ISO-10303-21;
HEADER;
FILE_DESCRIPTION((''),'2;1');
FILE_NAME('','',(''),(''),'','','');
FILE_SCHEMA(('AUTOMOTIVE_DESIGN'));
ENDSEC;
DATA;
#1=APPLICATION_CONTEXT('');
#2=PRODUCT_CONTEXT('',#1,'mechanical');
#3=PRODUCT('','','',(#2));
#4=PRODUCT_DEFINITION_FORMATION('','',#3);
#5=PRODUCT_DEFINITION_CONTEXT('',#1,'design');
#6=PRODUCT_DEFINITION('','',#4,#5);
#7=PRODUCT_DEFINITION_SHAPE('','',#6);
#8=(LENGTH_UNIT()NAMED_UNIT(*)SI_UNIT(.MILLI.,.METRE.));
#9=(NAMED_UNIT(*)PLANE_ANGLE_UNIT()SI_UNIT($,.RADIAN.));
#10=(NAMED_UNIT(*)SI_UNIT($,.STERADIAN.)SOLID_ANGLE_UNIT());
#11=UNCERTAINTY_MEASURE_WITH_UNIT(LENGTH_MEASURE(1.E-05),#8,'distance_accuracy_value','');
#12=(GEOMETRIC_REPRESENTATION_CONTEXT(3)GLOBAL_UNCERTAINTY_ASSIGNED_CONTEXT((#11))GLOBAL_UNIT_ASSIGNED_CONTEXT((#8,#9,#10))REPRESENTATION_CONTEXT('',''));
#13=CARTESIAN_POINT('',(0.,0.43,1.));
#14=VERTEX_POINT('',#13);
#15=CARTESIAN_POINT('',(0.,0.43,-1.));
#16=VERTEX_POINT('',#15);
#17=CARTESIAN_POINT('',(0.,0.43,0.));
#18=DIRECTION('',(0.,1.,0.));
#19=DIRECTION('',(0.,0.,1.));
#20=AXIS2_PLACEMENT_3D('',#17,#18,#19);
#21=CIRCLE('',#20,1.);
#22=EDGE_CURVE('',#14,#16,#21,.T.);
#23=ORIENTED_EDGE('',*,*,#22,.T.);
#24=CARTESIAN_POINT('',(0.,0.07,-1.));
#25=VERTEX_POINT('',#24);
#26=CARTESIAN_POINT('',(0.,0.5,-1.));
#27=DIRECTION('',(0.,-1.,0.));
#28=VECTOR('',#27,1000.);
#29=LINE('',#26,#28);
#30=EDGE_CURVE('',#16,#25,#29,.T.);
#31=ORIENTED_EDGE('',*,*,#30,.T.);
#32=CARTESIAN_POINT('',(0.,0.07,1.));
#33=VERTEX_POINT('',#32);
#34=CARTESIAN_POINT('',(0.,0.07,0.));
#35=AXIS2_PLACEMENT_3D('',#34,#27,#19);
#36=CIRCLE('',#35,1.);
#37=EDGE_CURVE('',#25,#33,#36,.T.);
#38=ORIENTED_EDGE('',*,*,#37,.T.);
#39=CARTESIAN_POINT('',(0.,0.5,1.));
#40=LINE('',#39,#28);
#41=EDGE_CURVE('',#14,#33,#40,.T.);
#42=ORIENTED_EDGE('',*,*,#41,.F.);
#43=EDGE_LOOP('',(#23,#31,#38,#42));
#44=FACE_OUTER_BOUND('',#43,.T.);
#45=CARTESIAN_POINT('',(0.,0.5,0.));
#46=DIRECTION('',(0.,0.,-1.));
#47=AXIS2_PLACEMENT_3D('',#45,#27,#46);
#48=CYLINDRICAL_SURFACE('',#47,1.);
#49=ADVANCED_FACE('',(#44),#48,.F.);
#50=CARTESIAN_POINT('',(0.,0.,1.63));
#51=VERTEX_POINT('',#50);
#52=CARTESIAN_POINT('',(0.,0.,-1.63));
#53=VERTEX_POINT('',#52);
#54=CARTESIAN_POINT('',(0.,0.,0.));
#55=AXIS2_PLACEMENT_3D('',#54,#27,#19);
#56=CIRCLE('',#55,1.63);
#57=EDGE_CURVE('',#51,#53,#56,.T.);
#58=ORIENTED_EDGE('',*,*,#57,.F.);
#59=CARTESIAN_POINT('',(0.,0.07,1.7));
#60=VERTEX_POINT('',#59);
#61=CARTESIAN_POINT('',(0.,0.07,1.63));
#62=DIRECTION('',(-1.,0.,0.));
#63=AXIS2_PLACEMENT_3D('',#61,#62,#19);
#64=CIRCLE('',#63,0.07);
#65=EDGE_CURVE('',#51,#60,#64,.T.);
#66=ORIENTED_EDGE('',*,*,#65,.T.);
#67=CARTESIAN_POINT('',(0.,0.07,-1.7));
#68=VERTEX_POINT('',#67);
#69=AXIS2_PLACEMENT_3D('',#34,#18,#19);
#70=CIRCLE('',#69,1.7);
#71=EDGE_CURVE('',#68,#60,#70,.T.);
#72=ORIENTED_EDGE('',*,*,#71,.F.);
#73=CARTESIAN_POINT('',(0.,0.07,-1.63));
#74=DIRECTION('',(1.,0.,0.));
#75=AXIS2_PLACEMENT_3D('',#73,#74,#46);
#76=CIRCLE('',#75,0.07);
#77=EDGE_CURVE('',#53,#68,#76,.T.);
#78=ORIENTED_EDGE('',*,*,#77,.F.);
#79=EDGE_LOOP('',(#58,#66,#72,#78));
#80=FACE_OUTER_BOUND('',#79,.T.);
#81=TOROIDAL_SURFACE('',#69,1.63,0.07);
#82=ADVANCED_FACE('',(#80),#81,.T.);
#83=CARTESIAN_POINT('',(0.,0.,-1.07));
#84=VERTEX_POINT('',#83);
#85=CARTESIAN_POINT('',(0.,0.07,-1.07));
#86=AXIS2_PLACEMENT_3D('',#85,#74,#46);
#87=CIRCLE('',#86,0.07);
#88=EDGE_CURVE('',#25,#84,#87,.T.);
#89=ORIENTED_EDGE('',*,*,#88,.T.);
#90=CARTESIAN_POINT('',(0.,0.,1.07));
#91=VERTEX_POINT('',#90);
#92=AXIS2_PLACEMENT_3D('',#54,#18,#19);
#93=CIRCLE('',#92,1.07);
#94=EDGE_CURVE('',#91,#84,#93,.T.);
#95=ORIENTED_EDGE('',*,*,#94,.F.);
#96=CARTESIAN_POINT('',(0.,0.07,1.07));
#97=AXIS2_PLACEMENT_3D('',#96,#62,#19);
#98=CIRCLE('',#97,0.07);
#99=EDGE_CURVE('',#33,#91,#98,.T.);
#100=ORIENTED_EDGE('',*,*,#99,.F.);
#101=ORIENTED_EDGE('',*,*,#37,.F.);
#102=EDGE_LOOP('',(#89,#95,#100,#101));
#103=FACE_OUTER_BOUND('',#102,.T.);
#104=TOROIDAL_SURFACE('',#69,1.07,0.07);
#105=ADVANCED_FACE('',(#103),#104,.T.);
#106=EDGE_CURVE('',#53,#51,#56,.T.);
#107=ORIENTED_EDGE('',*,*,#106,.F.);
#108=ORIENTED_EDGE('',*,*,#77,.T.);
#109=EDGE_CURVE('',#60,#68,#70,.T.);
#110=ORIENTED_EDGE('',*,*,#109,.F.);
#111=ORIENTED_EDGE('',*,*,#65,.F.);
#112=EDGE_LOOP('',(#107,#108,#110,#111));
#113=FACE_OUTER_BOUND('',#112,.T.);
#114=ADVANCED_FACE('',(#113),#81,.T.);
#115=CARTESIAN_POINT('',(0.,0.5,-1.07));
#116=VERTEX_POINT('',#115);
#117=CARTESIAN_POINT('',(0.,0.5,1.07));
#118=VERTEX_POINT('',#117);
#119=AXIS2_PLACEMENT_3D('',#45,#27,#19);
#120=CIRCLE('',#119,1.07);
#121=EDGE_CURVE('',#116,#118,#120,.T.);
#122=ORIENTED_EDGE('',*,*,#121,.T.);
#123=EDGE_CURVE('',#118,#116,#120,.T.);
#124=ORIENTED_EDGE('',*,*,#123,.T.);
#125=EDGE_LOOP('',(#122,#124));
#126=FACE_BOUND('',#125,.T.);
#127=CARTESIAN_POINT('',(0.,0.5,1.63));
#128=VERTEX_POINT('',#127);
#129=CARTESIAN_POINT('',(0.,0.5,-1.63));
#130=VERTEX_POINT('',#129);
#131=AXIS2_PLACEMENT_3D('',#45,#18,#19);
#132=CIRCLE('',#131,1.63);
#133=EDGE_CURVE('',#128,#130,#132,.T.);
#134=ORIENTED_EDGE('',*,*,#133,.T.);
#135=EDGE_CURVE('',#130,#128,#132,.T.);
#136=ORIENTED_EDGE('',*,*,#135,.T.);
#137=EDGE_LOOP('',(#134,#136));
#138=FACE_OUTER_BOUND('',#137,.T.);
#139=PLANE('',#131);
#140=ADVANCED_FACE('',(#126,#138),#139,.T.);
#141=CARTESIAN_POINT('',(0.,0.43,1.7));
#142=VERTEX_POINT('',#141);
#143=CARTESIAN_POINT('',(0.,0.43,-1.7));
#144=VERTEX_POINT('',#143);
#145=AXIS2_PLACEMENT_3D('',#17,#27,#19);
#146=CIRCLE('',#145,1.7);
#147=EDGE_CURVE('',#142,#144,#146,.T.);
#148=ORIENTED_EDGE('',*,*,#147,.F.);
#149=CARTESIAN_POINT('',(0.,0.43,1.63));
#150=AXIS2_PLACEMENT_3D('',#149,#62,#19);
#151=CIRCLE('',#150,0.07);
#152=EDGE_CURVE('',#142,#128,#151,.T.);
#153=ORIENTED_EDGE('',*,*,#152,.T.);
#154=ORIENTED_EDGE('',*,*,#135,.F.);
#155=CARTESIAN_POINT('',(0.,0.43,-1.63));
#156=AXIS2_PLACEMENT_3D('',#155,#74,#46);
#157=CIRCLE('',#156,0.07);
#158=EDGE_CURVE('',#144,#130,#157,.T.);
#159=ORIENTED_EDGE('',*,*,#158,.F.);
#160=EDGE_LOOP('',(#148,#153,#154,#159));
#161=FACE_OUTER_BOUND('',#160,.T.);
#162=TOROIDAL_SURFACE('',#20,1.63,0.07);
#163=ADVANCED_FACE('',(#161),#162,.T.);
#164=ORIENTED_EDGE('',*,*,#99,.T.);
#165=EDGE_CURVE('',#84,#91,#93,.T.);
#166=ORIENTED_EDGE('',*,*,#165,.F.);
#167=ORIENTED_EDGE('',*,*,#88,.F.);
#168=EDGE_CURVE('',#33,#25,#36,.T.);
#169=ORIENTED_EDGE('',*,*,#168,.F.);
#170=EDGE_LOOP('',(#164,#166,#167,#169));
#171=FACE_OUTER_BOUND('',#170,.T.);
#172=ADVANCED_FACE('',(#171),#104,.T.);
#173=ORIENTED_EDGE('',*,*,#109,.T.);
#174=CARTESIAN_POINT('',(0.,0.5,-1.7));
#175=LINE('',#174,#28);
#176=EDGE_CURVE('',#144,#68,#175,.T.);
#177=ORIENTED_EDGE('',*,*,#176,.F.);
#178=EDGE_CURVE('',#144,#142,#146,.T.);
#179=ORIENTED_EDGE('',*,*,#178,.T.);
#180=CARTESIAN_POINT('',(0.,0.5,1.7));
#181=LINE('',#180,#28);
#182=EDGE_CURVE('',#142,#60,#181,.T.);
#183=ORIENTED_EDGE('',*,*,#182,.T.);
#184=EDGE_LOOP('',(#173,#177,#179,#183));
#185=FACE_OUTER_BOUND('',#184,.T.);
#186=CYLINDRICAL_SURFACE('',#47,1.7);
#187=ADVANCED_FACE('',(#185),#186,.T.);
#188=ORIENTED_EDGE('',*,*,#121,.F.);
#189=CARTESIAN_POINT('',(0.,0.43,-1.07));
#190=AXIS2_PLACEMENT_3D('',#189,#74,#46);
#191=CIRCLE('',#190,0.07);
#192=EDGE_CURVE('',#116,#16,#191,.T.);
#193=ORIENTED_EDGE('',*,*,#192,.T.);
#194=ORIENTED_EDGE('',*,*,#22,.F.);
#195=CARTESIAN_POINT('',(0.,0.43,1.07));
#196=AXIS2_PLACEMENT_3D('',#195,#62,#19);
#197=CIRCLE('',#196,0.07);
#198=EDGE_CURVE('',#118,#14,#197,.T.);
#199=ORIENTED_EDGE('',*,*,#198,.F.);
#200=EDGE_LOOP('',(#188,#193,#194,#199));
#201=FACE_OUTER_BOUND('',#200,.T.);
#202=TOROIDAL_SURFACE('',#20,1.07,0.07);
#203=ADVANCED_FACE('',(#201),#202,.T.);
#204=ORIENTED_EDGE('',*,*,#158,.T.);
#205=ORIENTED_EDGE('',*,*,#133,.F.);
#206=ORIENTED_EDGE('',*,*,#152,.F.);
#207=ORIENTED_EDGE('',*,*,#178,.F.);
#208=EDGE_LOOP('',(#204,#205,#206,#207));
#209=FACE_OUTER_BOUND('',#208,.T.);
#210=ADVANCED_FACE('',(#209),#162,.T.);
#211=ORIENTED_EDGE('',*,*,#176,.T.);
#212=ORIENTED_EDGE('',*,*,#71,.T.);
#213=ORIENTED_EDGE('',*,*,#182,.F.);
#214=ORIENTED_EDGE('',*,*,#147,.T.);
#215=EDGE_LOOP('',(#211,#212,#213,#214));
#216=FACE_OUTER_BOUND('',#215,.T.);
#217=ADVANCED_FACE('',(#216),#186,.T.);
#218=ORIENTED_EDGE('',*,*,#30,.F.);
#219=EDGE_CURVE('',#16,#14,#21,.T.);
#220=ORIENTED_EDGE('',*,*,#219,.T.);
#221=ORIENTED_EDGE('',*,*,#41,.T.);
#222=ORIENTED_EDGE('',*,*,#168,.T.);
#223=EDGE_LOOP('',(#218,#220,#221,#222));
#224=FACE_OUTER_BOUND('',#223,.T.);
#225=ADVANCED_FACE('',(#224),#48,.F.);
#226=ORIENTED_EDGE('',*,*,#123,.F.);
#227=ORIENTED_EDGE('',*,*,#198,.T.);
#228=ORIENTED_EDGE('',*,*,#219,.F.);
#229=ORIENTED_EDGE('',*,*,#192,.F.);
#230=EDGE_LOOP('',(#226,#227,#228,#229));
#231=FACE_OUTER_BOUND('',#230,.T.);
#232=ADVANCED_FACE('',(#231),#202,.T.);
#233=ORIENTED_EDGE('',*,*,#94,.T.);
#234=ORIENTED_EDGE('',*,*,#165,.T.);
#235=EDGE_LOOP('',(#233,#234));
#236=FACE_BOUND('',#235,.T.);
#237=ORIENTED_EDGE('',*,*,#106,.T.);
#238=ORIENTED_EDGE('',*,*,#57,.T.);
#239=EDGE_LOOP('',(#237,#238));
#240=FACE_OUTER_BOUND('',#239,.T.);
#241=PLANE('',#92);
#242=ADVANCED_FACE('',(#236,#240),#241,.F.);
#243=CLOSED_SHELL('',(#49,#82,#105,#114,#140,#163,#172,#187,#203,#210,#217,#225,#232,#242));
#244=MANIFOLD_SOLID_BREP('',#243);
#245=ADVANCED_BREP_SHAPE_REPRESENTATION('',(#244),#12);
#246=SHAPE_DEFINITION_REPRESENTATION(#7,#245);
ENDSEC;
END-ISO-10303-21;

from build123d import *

# Parameters (mm, degrees)
SKETCH_1_R      = 1.7
SKETCH_1_R_2    = 1
EXTRUDE_1_DEPTH = 0.5
FILLET_1_R      = 0.07


with BuildPart() as part:
    # 草图1 → 凸台-拉伸1 (new body)
    with BuildSketch(Plane(origin=(0, 0, 0), x_dir=(1, 0, 0), z_dir=(0, 1, 0))):
        with Locations(Location((0, 0, 0), (0, 0, 270))):
            Circle(SKETCH_1_R)
        with Locations(Location((0, 0, 0), (0, 0, 270))):
            Circle(SKETCH_1_R_2, mode=Mode.SUBTRACT)
    extrude(amount=EXTRUDE_1_DEPTH)

    # 圆角1
    fillet_1_edges = [part.edges().sort_by_distance(p)[0] for p in [
        (0, 0, -1.7),
        (0, 0.5, -1.7),
        (0, 0, -1),
        (0, 0.5, -1),
    ]]
    fillet(fillet_1_edges, radius=FILLET_1_R)


solid = part.part
